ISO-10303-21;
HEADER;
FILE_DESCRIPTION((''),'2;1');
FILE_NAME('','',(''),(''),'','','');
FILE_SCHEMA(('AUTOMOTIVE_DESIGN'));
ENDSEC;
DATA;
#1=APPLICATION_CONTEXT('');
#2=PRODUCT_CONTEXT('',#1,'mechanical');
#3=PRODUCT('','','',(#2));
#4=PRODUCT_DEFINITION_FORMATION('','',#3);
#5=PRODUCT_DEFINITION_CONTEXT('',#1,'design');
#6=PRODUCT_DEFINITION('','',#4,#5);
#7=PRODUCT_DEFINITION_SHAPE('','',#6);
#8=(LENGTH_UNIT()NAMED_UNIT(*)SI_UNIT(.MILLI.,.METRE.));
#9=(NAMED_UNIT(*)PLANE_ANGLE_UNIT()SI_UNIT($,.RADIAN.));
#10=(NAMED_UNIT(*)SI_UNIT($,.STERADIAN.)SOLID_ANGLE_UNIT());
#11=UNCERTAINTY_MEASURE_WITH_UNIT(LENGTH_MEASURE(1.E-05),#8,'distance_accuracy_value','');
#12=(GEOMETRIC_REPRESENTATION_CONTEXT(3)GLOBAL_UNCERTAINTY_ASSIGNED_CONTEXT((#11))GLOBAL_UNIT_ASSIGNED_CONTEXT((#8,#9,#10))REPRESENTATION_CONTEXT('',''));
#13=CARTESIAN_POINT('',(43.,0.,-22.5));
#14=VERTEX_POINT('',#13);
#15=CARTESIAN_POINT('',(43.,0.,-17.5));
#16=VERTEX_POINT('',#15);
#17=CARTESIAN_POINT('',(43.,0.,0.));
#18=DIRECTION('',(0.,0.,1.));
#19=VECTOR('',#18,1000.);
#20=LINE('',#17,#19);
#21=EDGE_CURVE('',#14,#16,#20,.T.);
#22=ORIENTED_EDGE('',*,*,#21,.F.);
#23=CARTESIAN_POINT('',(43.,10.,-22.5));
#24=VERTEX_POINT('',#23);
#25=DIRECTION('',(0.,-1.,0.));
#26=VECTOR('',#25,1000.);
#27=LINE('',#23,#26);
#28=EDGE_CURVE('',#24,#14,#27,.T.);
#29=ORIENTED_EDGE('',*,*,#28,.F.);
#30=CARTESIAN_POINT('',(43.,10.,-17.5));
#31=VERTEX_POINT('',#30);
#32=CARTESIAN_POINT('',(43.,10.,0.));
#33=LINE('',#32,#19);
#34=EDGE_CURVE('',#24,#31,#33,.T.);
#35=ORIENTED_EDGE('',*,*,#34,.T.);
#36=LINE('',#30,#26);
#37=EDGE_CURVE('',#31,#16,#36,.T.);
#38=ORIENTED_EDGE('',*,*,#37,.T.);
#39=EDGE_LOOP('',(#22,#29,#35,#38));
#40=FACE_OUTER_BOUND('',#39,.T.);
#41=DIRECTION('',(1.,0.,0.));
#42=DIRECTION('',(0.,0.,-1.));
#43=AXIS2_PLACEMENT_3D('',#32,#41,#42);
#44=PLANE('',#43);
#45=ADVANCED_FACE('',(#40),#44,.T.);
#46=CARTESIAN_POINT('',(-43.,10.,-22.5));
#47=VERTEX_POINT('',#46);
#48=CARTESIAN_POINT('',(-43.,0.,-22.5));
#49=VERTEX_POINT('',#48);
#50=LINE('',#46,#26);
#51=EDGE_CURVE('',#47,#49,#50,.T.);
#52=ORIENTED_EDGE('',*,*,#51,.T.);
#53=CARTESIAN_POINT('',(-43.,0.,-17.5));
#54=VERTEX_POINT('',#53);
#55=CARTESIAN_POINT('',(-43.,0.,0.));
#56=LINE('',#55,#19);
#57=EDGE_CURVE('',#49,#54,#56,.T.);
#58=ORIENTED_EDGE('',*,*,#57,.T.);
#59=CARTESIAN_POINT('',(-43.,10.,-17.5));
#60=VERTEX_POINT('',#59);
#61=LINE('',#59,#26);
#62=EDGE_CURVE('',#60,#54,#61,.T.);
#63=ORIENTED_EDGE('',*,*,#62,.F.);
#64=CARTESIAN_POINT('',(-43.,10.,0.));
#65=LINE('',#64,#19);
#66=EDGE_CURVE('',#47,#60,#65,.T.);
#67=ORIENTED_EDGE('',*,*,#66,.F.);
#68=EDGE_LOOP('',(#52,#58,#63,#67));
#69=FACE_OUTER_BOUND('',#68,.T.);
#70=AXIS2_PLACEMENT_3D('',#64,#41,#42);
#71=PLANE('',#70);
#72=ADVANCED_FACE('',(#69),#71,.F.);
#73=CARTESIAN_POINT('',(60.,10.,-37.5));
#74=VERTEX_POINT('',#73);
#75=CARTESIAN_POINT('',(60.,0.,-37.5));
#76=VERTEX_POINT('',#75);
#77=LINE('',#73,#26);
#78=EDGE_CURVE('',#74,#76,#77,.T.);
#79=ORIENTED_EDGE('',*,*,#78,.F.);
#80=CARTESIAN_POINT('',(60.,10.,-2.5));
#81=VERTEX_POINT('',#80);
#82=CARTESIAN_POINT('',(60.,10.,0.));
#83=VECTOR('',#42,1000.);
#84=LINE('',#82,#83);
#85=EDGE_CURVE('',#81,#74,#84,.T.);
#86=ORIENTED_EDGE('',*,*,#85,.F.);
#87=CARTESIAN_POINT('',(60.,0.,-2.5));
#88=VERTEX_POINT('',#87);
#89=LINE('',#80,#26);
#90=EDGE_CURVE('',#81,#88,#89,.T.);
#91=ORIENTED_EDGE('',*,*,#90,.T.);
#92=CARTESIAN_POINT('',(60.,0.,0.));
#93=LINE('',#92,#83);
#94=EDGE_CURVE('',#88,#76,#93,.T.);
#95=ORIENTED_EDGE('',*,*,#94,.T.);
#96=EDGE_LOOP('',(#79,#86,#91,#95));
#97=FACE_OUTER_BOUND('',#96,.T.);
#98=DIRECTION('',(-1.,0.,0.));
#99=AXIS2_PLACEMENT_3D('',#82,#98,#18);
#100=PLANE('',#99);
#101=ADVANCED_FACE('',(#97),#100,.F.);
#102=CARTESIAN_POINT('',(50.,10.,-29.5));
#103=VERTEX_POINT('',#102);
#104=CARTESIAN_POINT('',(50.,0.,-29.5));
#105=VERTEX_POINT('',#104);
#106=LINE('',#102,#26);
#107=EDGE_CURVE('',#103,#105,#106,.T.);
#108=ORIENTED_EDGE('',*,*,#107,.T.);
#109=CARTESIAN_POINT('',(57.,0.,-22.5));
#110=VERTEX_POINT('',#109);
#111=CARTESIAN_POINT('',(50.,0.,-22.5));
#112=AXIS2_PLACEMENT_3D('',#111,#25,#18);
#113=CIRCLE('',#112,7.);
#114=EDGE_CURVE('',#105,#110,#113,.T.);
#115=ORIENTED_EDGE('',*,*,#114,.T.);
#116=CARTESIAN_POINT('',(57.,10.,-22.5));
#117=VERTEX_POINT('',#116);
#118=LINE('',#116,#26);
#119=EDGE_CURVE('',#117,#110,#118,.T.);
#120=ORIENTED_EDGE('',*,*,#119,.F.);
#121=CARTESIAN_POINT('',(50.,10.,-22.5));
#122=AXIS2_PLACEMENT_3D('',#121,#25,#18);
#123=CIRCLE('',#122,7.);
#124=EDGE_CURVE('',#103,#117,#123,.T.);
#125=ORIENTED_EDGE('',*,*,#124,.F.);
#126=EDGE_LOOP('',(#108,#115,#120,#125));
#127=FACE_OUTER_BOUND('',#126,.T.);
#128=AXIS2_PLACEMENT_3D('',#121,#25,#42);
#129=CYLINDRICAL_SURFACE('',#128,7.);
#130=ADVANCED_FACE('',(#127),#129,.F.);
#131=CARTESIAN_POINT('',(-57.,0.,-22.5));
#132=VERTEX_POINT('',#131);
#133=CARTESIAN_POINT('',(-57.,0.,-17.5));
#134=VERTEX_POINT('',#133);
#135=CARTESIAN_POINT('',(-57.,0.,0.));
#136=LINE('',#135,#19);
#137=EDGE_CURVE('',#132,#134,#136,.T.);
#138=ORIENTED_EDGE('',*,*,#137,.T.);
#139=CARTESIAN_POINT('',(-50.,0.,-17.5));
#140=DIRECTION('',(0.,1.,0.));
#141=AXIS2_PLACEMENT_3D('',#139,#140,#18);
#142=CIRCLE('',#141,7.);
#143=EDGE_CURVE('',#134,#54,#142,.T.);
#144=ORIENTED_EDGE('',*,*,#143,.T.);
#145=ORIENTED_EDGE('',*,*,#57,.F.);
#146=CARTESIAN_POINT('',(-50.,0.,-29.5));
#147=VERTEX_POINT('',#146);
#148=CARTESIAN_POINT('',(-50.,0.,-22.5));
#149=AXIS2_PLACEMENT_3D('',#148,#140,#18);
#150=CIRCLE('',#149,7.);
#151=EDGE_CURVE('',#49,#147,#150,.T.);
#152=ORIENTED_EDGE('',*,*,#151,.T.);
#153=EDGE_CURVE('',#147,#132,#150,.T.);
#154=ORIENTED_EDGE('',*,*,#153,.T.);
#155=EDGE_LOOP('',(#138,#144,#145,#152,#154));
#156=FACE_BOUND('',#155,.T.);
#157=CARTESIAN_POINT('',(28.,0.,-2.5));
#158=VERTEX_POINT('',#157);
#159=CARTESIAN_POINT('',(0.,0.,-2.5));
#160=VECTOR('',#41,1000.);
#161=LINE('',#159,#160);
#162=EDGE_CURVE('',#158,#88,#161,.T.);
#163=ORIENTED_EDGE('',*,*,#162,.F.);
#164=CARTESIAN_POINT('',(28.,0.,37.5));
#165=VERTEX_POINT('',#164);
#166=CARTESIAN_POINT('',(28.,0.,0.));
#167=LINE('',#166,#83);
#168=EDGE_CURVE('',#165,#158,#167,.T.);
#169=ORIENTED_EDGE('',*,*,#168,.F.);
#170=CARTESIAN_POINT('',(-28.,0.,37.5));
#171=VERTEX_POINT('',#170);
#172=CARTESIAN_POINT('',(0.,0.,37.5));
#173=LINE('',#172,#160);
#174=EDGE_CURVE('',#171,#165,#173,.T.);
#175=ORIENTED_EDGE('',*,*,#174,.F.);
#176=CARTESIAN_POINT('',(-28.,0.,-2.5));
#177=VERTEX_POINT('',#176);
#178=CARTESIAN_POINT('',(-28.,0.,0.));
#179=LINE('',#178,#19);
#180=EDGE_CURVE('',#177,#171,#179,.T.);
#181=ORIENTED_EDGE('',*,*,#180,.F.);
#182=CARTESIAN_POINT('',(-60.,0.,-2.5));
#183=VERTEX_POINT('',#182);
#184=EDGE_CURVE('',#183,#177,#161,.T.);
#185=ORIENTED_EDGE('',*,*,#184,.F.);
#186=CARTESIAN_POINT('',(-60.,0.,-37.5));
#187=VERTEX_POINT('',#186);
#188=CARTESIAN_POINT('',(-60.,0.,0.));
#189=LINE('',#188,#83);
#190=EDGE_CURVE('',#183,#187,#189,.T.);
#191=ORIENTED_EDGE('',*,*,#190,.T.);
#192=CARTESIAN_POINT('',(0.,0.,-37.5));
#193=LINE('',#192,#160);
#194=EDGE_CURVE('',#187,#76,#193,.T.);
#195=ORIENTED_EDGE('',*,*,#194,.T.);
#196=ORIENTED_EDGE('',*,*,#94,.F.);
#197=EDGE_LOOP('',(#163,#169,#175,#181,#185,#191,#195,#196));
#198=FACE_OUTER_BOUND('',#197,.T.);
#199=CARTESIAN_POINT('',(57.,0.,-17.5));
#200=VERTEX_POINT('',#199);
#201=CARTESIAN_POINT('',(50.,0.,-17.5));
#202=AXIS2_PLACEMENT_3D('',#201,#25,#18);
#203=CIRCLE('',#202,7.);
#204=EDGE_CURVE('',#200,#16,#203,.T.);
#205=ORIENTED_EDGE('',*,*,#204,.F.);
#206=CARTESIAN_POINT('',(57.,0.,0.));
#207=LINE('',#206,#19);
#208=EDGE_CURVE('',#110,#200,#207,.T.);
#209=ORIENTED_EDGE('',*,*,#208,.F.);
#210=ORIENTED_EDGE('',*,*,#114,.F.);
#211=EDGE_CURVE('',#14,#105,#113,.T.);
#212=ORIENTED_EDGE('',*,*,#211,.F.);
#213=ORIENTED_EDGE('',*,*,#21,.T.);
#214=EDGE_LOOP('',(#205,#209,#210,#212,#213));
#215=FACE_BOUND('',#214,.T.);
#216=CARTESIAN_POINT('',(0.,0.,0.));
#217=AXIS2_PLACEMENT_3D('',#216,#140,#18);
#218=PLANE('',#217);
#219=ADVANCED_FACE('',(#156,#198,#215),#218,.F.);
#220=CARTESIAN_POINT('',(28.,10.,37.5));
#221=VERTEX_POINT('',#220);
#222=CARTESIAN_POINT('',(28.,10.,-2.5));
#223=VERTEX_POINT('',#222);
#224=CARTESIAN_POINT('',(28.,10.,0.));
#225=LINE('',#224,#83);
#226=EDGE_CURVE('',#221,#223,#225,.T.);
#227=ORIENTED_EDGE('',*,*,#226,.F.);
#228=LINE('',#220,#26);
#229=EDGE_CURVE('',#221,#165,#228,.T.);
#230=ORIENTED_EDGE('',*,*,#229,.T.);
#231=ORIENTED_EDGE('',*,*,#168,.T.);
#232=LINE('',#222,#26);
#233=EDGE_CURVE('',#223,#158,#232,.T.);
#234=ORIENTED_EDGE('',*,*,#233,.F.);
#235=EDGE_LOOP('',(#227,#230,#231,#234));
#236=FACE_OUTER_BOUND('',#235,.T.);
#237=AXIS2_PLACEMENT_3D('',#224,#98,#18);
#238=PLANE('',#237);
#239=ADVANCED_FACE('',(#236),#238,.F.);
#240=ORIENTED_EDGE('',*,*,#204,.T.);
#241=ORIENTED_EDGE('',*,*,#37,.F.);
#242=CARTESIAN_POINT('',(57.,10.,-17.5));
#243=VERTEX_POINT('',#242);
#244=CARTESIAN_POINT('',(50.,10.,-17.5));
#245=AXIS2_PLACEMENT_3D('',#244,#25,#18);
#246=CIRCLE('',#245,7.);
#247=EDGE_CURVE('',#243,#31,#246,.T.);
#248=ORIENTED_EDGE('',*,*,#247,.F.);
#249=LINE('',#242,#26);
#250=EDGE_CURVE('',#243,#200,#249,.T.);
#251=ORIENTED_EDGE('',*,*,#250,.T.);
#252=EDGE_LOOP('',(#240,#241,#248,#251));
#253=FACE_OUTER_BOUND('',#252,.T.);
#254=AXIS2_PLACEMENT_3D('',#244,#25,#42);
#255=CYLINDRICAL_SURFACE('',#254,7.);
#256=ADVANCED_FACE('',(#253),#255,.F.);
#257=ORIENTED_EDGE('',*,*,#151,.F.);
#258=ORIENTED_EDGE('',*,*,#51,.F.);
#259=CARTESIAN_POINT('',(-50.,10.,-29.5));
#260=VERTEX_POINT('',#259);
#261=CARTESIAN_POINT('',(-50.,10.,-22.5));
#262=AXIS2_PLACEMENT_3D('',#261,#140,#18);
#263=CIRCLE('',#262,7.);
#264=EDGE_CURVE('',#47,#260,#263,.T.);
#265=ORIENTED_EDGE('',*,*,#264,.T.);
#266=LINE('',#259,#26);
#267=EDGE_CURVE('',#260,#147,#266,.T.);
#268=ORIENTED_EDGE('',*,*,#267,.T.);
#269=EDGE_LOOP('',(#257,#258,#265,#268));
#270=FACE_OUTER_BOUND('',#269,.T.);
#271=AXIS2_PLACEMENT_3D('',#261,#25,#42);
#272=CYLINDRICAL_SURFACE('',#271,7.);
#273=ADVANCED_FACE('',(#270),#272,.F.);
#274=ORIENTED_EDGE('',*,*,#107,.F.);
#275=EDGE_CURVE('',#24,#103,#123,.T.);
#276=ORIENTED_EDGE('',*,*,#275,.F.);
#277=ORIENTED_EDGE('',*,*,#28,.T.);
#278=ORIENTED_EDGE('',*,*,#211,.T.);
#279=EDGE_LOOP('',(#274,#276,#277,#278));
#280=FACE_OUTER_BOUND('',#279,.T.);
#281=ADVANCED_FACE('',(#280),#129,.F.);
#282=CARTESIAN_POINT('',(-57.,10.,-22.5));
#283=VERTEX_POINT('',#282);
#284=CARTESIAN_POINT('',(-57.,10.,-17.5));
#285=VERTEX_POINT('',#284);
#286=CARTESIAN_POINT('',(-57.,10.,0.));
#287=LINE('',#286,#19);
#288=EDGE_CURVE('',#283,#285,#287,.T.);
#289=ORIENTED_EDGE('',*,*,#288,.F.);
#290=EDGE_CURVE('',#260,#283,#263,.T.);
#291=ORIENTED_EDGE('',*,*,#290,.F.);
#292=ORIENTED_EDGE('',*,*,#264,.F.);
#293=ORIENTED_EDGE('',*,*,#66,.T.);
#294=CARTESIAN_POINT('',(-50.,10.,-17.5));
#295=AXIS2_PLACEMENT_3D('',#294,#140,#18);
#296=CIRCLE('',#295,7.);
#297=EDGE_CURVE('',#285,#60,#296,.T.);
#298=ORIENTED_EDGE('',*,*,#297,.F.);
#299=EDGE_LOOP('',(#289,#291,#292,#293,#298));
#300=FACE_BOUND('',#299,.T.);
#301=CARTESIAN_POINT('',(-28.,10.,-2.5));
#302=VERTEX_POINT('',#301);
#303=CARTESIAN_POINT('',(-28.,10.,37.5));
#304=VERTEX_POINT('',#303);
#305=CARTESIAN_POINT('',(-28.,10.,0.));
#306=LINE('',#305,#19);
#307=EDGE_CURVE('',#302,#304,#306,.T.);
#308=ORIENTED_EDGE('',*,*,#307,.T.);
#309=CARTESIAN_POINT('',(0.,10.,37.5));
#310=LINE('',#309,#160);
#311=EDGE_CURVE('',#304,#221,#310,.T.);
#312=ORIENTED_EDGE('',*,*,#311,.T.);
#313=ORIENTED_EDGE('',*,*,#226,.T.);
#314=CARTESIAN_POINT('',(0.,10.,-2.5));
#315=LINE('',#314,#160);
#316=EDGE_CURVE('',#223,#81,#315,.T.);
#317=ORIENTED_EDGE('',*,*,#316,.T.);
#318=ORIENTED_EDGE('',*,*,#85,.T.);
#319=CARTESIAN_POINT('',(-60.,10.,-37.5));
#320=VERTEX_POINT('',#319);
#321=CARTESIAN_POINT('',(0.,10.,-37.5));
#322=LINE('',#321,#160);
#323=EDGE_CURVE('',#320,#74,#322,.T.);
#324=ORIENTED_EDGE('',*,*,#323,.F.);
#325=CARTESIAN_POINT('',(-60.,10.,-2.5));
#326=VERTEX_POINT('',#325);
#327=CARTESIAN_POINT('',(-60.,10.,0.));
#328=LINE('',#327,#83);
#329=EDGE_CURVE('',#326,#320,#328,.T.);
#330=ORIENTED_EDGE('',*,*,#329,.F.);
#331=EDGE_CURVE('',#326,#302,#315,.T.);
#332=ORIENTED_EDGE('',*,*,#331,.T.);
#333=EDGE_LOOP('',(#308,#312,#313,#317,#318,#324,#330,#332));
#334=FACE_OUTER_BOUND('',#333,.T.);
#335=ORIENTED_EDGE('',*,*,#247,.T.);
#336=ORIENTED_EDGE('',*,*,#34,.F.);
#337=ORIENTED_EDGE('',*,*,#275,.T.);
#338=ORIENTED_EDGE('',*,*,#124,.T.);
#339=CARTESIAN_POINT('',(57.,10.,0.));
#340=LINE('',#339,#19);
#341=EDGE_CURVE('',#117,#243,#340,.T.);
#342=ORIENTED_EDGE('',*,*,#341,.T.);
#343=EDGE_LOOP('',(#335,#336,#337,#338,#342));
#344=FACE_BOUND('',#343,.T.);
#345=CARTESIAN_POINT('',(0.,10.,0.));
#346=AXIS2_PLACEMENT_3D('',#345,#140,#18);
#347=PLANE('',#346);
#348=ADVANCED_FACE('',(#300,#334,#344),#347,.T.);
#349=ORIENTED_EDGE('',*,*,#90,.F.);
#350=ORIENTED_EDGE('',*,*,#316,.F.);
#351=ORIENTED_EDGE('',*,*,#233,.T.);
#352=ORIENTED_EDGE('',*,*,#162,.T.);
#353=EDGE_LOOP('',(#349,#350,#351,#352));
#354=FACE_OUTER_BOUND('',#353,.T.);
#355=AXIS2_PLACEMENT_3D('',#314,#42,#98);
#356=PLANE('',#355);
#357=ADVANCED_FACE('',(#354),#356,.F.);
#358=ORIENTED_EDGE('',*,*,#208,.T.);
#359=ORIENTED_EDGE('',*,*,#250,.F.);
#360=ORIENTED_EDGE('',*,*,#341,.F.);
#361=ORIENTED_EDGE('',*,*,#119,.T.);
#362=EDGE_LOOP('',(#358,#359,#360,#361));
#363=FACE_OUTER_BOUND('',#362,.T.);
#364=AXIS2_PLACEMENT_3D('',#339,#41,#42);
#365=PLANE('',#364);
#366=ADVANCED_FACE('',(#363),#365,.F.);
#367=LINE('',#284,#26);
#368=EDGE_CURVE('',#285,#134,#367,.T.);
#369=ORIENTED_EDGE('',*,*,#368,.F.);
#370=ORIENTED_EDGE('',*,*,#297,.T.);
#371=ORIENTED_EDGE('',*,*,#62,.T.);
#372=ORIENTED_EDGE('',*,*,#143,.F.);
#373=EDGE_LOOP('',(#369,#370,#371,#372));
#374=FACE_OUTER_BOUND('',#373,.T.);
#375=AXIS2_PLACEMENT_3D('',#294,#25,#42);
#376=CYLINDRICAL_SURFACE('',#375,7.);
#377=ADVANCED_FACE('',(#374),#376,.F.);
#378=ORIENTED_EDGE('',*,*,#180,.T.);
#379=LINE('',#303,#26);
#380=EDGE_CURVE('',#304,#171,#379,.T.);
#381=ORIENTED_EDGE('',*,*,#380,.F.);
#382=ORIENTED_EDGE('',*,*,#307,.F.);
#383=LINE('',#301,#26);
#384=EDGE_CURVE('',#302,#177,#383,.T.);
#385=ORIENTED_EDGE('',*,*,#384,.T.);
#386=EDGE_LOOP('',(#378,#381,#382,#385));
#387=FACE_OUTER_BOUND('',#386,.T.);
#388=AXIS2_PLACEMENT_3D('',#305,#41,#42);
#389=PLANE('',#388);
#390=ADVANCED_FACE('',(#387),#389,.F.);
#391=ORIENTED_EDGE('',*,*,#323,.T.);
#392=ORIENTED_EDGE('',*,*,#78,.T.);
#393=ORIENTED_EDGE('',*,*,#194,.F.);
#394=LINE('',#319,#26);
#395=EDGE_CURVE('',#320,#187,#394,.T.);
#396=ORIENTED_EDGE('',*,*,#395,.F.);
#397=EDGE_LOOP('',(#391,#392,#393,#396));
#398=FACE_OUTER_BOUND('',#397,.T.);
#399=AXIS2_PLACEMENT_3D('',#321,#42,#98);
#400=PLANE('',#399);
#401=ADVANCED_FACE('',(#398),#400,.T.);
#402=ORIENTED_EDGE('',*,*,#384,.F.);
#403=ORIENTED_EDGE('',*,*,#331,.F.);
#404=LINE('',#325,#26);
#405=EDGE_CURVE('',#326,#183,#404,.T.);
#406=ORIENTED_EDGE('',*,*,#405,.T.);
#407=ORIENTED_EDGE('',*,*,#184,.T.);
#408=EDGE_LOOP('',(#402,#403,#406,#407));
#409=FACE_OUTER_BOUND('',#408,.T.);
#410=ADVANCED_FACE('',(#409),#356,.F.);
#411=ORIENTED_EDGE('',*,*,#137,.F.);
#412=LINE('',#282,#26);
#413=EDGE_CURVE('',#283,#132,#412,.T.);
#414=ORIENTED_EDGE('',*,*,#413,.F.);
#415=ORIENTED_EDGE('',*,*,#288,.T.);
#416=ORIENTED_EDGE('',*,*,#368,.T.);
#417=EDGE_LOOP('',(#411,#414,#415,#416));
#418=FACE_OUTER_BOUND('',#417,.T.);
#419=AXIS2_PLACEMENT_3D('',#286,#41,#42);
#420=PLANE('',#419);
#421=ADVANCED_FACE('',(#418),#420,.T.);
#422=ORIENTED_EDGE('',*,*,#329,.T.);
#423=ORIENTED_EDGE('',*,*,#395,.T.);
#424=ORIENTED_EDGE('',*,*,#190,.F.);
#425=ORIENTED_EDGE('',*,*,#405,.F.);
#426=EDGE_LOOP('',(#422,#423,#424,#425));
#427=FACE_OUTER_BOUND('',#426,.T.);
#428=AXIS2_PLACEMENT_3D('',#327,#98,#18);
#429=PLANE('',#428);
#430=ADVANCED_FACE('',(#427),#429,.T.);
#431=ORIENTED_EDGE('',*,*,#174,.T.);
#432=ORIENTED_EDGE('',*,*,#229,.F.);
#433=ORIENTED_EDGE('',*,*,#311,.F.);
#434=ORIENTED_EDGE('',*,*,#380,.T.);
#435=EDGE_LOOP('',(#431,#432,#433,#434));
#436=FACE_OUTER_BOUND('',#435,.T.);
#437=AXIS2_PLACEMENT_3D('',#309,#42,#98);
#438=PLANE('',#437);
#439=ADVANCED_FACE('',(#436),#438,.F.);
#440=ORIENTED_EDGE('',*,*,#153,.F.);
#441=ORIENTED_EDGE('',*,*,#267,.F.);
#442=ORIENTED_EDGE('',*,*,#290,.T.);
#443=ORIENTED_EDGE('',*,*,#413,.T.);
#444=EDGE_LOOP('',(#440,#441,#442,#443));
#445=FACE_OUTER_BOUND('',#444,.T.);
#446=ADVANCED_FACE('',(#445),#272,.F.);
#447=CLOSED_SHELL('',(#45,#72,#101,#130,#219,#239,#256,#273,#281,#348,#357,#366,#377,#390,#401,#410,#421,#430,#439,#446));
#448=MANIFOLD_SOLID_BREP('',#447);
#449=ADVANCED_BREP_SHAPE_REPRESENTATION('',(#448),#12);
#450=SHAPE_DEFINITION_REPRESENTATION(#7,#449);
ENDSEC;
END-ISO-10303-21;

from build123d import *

# Parameters (mm, degrees)
BOSS_EXTRUDE1_DEPTH = 10


with BuildPart() as part:
    # Sketch1 → Boss-Extrude1 (new body)
    with BuildSketch(Plane(origin=(0, 0, 0), x_dir=(1, 0, 0), z_dir=(0, 1, 0))):
        Polygon((-60, 37.5), (-60, 2.5), (-28, 2.5), (-28, -37.5), (28, -37.5), (28, 2.5), (60, 2.5), (60, 37.5), align=None)
        with BuildLine():
            ThreePointArc((-57, 22.5), (-50, 29.5), (-43, 22.5))
            Line((-43, 22.5), (-43, 17.5))
            ThreePointArc((-43, 17.5), (-50, 10.5), (-57, 17.5))
            Line((-57, 17.5), (-57, 22.5))
        make_face(mode=Mode.SUBTRACT)
        with BuildLine():
            Line((43, 17.5), (43, 22.5))
            ThreePointArc((43, 22.5), (50, 29.5), (57, 22.5))
            Line((57, 22.5), (57, 17.5))
            ThreePointArc((57, 17.5), (50, 10.5), (43, 17.5))
        make_face(mode=Mode.SUBTRACT)
    extrude(amount=BOSS_EXTRUDE1_DEPTH)


solid = part.part
